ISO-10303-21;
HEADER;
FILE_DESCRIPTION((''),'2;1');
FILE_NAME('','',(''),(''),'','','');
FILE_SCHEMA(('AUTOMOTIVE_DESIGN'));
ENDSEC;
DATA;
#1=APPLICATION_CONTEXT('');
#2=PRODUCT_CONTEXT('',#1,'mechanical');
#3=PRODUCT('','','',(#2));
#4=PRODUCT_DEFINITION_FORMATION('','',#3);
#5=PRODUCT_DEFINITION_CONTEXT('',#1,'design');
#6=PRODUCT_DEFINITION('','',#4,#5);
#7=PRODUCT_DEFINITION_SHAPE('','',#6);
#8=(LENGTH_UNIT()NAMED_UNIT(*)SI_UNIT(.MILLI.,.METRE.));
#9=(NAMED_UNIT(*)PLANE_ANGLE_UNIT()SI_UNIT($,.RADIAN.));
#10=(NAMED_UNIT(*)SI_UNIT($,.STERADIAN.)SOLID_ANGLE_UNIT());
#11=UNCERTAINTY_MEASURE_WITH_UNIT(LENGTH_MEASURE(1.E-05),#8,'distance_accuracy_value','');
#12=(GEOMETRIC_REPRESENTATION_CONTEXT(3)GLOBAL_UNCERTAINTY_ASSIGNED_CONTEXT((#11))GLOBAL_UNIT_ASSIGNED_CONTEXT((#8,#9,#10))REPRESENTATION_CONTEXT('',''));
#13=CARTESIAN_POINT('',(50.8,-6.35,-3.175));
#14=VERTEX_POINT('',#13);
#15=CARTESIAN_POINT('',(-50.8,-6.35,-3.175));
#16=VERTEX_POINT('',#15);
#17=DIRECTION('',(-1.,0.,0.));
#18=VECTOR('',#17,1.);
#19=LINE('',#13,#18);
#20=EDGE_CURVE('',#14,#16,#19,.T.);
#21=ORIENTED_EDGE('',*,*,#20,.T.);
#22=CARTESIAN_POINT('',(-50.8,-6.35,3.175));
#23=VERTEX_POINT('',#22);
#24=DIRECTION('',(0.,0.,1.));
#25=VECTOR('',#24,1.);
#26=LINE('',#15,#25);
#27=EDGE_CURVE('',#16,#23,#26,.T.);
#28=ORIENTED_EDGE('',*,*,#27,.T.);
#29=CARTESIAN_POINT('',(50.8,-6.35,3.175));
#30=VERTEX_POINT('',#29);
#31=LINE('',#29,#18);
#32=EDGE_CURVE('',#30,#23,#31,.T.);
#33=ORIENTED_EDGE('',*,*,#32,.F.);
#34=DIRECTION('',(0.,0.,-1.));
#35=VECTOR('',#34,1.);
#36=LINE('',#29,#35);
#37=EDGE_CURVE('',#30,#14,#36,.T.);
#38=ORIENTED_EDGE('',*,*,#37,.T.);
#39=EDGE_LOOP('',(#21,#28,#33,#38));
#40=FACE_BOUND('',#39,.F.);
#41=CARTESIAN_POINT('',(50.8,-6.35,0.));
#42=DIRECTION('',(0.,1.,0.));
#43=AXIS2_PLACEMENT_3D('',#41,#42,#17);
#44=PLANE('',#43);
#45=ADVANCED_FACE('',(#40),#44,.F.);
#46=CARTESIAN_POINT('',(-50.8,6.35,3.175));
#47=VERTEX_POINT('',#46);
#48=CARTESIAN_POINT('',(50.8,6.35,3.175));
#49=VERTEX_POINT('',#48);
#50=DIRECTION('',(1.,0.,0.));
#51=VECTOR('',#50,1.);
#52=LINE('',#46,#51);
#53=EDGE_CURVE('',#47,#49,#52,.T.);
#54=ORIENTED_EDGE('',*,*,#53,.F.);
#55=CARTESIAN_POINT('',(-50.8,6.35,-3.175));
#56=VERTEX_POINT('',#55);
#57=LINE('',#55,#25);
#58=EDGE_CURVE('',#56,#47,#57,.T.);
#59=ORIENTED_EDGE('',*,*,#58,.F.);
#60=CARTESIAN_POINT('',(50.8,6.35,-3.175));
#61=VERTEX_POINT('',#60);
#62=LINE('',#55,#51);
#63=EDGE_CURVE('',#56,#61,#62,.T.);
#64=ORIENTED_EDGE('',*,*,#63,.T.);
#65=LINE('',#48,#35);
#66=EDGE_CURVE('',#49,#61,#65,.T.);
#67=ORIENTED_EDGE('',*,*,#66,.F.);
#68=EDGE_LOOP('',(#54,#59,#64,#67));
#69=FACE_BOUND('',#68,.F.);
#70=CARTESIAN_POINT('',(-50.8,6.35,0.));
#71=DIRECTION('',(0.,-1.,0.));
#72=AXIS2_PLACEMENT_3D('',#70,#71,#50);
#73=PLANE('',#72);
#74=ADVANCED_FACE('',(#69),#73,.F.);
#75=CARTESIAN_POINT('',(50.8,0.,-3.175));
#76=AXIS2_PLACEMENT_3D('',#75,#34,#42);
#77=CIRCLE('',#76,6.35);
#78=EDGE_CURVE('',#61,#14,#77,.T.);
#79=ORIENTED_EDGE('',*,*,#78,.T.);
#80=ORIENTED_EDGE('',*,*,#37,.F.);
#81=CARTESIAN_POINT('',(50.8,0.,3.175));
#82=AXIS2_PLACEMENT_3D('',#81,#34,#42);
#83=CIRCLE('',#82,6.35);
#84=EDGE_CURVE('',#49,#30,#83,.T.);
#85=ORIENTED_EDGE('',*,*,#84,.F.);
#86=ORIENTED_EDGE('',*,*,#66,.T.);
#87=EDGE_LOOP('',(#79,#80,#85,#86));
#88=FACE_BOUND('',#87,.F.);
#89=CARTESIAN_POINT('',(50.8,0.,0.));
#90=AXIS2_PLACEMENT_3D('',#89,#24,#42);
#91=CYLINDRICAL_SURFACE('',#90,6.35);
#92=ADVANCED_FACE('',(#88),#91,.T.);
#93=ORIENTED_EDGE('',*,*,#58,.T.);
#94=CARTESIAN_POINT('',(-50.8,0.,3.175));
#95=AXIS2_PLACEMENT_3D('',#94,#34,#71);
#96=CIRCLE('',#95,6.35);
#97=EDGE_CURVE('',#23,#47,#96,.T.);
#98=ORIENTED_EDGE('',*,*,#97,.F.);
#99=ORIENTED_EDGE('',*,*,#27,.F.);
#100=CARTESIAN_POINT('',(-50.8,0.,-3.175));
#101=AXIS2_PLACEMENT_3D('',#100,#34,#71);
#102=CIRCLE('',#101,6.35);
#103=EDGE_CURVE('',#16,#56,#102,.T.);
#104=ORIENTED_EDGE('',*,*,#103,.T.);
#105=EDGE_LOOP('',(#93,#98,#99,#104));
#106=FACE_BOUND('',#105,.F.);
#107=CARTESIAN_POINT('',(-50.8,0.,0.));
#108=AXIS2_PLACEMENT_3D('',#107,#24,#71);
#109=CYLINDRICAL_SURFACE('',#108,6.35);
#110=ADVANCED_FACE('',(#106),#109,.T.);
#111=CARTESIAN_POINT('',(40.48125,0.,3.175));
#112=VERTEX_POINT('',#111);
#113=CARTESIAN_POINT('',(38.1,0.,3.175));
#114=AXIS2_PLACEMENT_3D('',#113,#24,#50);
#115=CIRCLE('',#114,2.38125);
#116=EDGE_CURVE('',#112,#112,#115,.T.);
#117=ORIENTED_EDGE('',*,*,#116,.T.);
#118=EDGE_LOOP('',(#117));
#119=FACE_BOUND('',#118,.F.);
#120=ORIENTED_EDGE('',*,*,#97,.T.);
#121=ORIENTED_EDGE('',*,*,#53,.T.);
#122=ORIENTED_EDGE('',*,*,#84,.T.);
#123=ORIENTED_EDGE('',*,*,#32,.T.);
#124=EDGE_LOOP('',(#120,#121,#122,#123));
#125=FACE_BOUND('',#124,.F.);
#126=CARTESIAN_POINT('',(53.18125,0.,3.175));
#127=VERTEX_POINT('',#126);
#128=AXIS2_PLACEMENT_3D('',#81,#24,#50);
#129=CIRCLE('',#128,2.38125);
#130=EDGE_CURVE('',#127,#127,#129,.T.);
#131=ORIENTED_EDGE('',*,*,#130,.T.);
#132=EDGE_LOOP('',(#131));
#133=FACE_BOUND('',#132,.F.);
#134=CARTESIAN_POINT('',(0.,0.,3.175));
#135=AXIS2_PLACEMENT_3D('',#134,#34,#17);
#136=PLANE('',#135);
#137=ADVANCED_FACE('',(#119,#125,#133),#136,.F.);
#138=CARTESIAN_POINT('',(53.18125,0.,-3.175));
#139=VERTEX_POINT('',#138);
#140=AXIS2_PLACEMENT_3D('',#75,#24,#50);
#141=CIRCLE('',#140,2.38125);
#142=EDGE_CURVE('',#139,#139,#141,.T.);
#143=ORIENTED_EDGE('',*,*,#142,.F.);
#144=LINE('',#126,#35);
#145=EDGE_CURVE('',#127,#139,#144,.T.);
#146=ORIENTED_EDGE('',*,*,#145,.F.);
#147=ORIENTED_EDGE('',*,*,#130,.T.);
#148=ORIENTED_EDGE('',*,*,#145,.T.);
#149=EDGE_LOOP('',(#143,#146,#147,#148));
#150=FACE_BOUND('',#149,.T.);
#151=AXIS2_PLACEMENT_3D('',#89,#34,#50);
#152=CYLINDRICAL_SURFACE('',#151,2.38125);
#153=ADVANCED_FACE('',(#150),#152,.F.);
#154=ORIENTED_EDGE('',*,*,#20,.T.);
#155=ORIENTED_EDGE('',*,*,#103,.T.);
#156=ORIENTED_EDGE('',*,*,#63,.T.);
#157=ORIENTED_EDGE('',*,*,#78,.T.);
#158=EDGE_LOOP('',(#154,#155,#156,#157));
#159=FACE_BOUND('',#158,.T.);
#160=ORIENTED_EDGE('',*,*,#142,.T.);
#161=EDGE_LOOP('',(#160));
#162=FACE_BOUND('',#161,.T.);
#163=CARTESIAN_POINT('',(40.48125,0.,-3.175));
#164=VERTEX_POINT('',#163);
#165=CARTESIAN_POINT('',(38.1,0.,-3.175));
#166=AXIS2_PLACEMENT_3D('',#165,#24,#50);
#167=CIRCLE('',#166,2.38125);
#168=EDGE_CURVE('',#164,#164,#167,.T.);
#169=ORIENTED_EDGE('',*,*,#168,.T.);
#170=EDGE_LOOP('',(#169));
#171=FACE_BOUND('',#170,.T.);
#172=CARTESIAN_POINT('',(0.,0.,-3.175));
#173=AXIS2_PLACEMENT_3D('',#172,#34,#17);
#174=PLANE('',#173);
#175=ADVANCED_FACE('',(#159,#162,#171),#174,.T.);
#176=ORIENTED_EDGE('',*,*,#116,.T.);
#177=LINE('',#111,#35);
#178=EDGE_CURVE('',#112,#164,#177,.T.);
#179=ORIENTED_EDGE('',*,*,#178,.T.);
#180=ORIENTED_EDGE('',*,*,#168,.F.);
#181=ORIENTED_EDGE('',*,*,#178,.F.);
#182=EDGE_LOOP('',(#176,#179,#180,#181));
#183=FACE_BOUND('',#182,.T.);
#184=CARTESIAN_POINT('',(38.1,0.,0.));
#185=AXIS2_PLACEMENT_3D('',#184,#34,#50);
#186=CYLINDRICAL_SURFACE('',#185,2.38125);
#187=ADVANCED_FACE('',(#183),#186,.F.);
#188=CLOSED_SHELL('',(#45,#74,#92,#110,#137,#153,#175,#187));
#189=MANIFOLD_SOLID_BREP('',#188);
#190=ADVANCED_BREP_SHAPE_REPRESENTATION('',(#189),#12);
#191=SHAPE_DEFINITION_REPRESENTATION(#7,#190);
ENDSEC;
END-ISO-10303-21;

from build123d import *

# Parameters (mm, degrees)
HANDLE_PROFILE_SKETCH_R        = 0.09375
HANDLE_BAR_EXTRUDE_DEPTH       = 0.125
SCALE_X25_4_TO_INCH_SIZE_SCALE = 25.4


with BuildPart() as part:
    # Handle Profile Sketch → Handle Bar Extrude (new, symmetric)
    with BuildSketch(Plane.XY):
        with BuildLine():
            Line((-2, 0.25), (2, 0.25))
            ThreePointArc((2, 0.25), (2.25, 0), (2, -0.25))
            Line((2, -0.25), (-2, -0.25))
            ThreePointArc((-2, -0.25), (-2.25, 0), (-2, 0.25))
        make_face()
        with Locations((2, 0)):
            Circle(HANDLE_PROFILE_SKETCH_R, mode=Mode.SUBTRACT)
        with Locations((1.5, 0)):
            Circle(HANDLE_PROFILE_SKETCH_R, mode=Mode.SUBTRACT)
    extrude(amount=HANDLE_BAR_EXTRUDE_DEPTH, both=True)


with BuildPart() as part_1:
    # Scale x25.4 to Inch Size: scaled about (0, 0, 0)
    add(part.part.scale(SCALE_X25_4_TO_INCH_SIZE_SCALE))


solid = part_1.part
